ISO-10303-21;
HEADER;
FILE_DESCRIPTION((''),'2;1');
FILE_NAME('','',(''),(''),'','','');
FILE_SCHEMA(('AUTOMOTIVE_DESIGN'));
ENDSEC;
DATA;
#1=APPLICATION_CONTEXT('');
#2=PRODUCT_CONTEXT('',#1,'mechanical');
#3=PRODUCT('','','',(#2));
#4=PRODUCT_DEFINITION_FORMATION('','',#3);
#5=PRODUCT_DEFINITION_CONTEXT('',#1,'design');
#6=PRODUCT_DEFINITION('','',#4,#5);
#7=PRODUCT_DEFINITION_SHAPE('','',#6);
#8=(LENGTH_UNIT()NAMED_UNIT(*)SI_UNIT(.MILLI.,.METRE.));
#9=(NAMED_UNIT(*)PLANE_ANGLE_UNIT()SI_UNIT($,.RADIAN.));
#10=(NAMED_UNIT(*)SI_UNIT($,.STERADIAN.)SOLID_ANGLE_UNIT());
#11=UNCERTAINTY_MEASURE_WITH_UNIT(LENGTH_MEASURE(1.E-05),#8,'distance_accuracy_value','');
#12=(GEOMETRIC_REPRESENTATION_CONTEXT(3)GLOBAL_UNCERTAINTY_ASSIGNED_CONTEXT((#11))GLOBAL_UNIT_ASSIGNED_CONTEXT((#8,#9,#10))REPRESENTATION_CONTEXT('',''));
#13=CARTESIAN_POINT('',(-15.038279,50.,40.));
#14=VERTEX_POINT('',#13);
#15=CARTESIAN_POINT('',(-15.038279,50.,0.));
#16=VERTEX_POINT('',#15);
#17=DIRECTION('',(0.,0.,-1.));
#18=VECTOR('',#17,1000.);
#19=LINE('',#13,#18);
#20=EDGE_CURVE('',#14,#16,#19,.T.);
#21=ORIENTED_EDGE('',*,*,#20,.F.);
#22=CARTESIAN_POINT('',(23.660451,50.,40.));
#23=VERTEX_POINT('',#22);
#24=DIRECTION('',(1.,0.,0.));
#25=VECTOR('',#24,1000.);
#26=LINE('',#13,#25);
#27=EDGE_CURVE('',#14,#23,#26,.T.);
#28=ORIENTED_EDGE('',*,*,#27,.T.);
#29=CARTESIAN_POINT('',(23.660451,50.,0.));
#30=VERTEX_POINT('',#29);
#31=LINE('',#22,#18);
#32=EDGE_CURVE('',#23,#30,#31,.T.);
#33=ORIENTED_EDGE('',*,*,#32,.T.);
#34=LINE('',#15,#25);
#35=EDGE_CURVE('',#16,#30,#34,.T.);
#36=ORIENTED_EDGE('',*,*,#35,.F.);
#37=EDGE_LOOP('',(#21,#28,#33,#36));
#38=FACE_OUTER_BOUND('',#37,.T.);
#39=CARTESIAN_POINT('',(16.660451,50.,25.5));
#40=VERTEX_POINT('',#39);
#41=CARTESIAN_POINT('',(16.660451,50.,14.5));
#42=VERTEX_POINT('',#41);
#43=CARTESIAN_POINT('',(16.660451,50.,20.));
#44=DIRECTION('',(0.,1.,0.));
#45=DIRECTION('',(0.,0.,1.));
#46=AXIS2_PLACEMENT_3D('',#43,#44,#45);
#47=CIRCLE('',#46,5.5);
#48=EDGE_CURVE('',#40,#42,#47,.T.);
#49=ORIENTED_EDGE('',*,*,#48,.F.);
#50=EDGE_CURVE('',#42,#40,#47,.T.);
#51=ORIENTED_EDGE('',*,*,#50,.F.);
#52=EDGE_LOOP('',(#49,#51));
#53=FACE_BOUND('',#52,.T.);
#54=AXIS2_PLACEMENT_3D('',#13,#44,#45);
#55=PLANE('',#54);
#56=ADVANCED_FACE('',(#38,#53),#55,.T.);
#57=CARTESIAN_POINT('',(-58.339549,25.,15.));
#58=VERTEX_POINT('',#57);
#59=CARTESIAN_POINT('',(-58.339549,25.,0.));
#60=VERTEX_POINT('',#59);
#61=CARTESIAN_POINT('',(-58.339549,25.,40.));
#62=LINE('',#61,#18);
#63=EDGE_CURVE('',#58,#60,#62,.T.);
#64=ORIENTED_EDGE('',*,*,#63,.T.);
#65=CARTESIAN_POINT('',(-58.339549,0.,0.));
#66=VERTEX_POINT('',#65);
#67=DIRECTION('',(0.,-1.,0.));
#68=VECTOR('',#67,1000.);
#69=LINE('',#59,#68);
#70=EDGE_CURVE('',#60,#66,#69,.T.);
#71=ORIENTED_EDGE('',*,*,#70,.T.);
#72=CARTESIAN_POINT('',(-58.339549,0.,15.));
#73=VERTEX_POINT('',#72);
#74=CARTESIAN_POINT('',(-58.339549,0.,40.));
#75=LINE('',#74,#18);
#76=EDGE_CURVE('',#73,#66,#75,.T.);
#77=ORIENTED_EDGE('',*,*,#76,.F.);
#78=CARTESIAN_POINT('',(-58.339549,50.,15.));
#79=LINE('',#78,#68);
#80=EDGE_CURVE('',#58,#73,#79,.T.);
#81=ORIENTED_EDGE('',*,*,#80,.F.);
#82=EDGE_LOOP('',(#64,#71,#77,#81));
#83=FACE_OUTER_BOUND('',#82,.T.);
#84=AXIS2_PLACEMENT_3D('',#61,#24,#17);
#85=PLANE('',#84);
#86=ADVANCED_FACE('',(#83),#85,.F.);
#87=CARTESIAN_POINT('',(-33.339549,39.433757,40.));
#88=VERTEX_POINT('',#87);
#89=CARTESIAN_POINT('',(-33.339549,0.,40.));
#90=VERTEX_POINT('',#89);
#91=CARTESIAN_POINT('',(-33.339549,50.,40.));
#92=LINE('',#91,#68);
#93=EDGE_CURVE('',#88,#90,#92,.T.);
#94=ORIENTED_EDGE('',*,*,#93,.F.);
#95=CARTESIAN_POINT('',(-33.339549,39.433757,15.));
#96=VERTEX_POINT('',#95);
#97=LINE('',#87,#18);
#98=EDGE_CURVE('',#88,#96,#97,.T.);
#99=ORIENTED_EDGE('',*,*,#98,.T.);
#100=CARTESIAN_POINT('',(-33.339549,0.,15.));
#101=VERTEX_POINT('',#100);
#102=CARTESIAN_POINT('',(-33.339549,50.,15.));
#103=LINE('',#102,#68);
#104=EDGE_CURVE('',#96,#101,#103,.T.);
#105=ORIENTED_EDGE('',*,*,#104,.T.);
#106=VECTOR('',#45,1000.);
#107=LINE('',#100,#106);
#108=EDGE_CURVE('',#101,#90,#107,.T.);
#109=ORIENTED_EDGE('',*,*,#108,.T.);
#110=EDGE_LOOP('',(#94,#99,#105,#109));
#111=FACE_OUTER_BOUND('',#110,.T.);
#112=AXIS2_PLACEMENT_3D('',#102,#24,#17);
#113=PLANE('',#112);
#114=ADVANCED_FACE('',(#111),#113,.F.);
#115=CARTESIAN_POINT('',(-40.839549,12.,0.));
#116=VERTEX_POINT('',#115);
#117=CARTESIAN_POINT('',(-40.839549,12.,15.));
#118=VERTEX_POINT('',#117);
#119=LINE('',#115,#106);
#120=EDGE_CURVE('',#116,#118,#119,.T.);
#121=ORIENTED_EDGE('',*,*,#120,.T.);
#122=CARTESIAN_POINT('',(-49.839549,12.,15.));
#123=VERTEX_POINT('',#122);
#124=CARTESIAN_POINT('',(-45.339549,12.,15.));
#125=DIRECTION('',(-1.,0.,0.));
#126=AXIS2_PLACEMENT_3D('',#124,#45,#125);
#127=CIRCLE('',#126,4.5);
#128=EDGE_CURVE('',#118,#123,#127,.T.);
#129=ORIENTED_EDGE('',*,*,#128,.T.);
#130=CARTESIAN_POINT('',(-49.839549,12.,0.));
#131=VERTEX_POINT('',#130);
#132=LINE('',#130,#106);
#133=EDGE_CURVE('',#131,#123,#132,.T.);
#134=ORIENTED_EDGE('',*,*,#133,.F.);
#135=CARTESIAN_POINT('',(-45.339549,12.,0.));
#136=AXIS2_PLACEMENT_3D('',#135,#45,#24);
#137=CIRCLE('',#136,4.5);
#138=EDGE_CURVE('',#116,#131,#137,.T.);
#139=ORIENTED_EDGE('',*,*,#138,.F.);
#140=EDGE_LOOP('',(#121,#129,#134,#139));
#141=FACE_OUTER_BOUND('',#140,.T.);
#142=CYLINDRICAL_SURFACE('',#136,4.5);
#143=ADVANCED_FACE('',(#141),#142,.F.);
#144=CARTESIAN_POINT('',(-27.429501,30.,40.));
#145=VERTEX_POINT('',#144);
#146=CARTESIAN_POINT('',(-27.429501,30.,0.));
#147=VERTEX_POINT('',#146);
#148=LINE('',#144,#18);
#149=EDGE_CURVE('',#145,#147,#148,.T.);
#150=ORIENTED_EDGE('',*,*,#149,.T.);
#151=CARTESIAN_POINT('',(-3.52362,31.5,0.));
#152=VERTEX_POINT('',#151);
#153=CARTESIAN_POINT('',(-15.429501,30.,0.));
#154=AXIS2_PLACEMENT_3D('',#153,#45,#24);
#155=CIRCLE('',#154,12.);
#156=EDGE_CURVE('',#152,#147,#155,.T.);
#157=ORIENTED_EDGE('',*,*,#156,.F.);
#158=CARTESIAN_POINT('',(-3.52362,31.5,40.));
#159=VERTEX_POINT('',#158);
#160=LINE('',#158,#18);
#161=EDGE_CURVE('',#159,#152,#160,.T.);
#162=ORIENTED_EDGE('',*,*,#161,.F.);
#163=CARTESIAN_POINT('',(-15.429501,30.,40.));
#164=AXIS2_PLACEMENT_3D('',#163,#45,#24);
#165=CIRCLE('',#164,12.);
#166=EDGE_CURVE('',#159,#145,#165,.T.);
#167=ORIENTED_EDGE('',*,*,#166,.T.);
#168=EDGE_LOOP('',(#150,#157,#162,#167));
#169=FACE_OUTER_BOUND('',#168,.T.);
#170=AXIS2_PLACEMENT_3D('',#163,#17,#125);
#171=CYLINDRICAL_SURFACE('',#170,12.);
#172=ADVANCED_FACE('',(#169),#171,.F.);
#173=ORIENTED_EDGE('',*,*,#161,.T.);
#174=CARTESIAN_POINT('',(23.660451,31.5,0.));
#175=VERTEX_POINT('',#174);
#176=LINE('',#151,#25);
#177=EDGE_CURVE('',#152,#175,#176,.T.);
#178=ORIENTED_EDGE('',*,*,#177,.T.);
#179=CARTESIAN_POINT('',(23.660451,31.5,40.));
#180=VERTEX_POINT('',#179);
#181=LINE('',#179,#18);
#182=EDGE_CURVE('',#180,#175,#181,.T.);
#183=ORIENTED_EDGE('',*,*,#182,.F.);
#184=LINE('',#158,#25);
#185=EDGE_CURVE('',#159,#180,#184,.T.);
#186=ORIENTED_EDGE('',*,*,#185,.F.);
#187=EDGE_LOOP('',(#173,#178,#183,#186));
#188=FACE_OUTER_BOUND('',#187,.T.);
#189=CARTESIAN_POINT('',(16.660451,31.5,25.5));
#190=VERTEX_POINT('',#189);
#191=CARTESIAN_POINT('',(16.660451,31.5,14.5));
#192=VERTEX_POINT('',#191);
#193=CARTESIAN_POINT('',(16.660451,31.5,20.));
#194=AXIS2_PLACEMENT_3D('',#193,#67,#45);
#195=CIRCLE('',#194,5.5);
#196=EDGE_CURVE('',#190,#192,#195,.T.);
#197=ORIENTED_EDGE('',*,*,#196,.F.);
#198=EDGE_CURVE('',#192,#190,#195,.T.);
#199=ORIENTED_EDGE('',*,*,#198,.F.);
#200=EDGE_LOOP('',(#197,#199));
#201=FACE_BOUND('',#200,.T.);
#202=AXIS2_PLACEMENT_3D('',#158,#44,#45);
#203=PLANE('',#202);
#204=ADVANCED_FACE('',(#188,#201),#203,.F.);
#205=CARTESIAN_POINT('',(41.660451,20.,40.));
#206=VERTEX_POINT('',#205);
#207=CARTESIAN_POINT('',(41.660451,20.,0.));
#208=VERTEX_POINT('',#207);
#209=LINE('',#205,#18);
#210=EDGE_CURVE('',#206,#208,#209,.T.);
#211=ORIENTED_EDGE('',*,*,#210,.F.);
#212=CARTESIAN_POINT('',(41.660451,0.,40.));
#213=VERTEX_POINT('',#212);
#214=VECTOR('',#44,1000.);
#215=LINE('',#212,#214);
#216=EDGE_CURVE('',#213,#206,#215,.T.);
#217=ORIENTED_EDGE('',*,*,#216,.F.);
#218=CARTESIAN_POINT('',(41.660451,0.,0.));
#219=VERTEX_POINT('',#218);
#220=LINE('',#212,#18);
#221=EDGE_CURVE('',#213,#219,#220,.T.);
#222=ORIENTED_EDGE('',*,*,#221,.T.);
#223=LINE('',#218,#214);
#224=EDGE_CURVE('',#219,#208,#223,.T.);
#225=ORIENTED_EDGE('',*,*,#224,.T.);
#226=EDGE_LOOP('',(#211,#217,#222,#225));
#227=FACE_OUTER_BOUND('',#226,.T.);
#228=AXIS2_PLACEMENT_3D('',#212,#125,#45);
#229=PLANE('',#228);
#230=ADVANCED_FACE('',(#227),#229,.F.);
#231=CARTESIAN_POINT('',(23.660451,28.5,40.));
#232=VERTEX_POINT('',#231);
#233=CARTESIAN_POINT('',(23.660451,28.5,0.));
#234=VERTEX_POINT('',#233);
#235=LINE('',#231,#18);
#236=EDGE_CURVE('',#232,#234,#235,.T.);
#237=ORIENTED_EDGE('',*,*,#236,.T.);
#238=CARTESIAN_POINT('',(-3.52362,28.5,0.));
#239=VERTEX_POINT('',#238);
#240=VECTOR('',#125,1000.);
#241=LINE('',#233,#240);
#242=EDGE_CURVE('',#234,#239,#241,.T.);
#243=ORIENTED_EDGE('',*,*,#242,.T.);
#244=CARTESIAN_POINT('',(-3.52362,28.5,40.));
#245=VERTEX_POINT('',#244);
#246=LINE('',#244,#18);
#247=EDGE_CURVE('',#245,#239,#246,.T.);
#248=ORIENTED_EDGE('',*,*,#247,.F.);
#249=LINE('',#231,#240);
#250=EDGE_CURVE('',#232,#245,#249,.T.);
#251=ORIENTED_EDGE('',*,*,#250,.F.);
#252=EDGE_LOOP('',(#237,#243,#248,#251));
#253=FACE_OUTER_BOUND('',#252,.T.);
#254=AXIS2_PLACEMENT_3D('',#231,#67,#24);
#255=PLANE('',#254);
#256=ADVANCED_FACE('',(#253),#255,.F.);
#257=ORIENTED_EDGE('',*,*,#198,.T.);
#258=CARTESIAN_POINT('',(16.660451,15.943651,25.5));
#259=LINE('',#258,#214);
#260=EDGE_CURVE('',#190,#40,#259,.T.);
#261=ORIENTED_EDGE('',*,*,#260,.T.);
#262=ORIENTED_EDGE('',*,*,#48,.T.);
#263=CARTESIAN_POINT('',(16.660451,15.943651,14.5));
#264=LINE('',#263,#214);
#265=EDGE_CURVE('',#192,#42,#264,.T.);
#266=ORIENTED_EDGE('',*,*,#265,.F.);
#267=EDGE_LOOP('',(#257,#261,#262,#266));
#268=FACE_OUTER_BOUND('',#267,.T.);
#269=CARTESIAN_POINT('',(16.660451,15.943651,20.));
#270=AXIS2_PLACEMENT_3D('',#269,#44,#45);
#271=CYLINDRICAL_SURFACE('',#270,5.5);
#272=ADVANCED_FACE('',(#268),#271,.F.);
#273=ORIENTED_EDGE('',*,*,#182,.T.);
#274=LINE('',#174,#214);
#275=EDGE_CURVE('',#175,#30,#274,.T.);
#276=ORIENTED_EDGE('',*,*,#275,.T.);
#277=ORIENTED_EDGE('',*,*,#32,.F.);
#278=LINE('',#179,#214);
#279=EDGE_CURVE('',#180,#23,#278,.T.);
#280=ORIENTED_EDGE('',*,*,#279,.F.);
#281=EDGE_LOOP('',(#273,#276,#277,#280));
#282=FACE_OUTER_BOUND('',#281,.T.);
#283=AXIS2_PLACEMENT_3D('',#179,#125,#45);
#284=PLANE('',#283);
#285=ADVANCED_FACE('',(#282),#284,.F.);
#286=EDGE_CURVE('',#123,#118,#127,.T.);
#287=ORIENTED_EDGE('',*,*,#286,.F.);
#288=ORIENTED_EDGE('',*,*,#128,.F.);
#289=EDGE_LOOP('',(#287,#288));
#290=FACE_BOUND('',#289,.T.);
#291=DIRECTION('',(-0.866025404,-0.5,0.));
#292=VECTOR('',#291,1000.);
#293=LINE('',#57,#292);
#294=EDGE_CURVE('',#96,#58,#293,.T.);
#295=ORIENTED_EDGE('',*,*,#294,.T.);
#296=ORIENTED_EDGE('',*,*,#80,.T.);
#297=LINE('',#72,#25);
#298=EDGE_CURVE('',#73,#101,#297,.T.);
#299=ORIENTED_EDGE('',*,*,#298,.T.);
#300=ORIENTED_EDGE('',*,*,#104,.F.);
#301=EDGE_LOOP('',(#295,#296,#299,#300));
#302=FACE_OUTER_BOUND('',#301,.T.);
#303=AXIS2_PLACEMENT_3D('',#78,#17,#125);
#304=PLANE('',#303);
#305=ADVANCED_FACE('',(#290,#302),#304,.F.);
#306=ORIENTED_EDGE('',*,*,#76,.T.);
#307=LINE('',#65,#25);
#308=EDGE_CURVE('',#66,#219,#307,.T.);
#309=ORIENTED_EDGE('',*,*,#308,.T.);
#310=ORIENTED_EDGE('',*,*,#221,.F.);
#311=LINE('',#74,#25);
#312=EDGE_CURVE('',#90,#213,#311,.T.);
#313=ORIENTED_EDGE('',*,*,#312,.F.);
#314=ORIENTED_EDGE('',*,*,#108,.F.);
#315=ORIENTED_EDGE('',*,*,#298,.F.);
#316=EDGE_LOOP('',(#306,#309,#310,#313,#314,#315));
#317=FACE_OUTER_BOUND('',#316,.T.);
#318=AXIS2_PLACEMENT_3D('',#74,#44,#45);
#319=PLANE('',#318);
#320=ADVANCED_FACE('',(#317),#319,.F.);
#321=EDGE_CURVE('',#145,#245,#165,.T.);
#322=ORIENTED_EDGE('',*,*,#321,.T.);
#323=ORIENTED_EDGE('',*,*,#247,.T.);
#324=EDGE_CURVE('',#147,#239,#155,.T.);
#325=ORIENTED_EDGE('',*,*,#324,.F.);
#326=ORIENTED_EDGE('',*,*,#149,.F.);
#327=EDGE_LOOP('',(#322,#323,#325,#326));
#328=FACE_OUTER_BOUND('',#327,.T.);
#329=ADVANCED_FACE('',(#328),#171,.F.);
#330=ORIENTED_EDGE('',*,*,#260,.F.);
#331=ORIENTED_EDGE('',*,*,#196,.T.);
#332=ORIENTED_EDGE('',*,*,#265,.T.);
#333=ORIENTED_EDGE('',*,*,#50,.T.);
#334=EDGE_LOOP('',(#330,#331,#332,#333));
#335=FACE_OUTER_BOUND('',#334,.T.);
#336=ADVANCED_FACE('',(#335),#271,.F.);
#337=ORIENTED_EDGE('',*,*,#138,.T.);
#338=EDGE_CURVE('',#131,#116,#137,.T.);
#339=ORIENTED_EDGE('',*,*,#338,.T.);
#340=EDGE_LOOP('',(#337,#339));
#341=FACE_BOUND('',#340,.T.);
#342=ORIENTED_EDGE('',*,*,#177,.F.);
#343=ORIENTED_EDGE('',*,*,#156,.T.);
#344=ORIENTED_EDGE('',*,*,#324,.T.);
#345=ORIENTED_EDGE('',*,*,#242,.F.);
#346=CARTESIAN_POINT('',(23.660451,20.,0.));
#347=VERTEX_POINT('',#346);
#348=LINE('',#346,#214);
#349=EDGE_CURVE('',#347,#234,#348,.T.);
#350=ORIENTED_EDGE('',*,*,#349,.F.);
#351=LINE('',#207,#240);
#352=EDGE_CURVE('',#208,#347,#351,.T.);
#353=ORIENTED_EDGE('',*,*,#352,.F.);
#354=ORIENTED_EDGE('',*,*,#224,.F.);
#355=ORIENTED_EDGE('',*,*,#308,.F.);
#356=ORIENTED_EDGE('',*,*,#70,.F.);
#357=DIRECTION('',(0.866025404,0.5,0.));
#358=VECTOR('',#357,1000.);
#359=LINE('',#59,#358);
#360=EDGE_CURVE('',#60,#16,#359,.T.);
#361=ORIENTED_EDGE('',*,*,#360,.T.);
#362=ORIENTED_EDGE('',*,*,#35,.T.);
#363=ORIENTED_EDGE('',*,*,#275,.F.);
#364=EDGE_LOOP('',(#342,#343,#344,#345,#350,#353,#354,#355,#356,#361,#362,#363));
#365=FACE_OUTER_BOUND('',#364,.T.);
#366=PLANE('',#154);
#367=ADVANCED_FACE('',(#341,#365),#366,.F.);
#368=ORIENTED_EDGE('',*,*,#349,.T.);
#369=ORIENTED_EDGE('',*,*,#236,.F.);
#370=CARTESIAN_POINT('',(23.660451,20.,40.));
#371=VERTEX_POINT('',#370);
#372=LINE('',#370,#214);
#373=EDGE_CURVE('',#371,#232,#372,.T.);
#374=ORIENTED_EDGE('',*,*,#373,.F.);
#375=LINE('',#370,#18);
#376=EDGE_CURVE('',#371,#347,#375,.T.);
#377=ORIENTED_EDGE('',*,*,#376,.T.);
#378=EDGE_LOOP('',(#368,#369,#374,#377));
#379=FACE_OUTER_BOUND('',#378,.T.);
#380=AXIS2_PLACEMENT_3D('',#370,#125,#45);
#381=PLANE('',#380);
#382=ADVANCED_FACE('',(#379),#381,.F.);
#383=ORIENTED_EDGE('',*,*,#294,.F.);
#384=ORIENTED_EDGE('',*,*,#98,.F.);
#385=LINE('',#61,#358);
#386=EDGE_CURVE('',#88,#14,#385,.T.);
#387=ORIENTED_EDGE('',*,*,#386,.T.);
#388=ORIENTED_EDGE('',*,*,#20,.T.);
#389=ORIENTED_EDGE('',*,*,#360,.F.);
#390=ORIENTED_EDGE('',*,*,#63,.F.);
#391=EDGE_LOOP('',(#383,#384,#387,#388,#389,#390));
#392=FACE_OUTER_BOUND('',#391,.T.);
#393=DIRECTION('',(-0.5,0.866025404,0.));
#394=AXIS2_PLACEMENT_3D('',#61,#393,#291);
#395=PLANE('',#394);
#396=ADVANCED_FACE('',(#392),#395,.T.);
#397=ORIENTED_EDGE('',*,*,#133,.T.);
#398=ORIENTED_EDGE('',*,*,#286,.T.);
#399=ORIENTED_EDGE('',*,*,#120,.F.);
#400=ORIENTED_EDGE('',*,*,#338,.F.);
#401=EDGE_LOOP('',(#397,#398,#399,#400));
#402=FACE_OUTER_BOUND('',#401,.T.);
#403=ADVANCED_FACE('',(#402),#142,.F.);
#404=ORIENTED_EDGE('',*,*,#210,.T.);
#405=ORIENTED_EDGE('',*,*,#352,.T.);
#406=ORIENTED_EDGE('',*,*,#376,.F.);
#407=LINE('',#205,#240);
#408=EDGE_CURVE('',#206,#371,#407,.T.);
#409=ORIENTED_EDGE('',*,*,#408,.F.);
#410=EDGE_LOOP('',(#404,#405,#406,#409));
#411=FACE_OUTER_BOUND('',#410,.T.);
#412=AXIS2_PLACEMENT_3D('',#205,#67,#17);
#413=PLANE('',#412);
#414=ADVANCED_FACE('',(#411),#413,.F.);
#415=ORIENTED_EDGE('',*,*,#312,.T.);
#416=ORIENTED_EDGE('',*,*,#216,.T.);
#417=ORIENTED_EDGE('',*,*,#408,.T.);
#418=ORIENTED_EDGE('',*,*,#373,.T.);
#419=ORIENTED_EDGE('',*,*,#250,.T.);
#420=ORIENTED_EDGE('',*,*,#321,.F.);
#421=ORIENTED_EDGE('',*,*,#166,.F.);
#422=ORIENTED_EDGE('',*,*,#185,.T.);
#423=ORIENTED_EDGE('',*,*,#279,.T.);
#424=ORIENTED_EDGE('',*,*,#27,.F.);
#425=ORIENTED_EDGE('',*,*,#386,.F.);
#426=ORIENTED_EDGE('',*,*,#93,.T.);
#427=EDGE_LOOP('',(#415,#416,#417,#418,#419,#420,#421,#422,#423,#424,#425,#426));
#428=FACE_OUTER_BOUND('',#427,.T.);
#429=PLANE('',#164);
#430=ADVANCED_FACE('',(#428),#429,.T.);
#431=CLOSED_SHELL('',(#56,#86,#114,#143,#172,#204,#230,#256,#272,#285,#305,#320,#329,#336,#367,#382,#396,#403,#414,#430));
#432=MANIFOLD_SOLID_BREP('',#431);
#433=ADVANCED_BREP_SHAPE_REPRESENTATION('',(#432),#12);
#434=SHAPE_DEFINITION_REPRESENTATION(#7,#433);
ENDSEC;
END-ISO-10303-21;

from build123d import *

# Parameters (mm, degrees)
BLOCK_BODY_DEPTH            = 40
CROSS_HOLE_SKETCH_R         = 4.5
CROSS_HOLE_DEPTH            = 87.622762369
RECTANGULAR_CUT_SKETCH_W    = 25
RECTANGULAR_CUT_SKETCH_H    = 25
RECTANGULAR_CUT_15X75_DEPTH = 87.622762369
TOP_CLAMP_HOLE_SKETCH_R     = 5.5
TOP_CLAMP_HOLE_DEPTH        = 18.5


with BuildPart() as part:
    # Block Profile Sketch → Block Body (new body)
    with BuildSketch(Plane.XY):
        with BuildLine():
            Line((-58.339548854, 25), (-58.339548854, 0))
            Line((-58.339548854, 0), (41.660451146, 0))
            Line((41.660451146, 0), (41.660451146, 20))
            Line((41.660451146, 20), (23.660451146, 20))
            Line((23.660451146, 20), (23.660451146, 28.5))
            Line((23.660451146, 28.5), (-3.52361978, 28.5))
            ThreePointArc((-3.52361978, 28.5), (-27.42950068, 30), (-3.52361978, 31.5))
            Line((-3.52361978, 31.5), (23.660451146, 31.5))
            Line((23.660451146, 31.5), (23.660451146, 50))
            Line((23.660451146, 50), (-15.038278665, 50))
            Line((-15.038278665, 50), (-58.339548854, 25))
        make_face()
    extrude(amount=BLOCK_BODY_DEPTH)

    # Cross Hole Sketch → Cross Hole (cut, through all)
    with BuildSketch(Plane.XY.offset(40)):
        with Locations((-45.339548854, 12)):
            Circle(CROSS_HOLE_SKETCH_R)
    extrude(amount=-CROSS_HOLE_DEPTH, mode=Mode.SUBTRACT)

    # Rectangular Cut Sketch → Rectangular Cut 15x75 (cut, through all)
    with BuildSketch(Plane.XZ):
        with Locations((-45.839548854, 27.5)):
            Rectangle(RECTANGULAR_CUT_SKETCH_W, RECTANGULAR_CUT_SKETCH_H)
    extrude(amount=-RECTANGULAR_CUT_15X75_DEPTH, mode=Mode.SUBTRACT)

    # Top Clamp Hole Sketch → Top Clamp Hole (cut)
    with BuildSketch(Plane(origin=(0, 50, 0), x_dir=(1, 0, 0), z_dir=(0, 1, 0))):
        with Locations(Location((16.660451146, -20, 0), (0, 0, 270))):
            Circle(TOP_CLAMP_HOLE_SKETCH_R)
    extrude(amount=-TOP_CLAMP_HOLE_DEPTH, mode=Mode.SUBTRACT)


solid = part.part
